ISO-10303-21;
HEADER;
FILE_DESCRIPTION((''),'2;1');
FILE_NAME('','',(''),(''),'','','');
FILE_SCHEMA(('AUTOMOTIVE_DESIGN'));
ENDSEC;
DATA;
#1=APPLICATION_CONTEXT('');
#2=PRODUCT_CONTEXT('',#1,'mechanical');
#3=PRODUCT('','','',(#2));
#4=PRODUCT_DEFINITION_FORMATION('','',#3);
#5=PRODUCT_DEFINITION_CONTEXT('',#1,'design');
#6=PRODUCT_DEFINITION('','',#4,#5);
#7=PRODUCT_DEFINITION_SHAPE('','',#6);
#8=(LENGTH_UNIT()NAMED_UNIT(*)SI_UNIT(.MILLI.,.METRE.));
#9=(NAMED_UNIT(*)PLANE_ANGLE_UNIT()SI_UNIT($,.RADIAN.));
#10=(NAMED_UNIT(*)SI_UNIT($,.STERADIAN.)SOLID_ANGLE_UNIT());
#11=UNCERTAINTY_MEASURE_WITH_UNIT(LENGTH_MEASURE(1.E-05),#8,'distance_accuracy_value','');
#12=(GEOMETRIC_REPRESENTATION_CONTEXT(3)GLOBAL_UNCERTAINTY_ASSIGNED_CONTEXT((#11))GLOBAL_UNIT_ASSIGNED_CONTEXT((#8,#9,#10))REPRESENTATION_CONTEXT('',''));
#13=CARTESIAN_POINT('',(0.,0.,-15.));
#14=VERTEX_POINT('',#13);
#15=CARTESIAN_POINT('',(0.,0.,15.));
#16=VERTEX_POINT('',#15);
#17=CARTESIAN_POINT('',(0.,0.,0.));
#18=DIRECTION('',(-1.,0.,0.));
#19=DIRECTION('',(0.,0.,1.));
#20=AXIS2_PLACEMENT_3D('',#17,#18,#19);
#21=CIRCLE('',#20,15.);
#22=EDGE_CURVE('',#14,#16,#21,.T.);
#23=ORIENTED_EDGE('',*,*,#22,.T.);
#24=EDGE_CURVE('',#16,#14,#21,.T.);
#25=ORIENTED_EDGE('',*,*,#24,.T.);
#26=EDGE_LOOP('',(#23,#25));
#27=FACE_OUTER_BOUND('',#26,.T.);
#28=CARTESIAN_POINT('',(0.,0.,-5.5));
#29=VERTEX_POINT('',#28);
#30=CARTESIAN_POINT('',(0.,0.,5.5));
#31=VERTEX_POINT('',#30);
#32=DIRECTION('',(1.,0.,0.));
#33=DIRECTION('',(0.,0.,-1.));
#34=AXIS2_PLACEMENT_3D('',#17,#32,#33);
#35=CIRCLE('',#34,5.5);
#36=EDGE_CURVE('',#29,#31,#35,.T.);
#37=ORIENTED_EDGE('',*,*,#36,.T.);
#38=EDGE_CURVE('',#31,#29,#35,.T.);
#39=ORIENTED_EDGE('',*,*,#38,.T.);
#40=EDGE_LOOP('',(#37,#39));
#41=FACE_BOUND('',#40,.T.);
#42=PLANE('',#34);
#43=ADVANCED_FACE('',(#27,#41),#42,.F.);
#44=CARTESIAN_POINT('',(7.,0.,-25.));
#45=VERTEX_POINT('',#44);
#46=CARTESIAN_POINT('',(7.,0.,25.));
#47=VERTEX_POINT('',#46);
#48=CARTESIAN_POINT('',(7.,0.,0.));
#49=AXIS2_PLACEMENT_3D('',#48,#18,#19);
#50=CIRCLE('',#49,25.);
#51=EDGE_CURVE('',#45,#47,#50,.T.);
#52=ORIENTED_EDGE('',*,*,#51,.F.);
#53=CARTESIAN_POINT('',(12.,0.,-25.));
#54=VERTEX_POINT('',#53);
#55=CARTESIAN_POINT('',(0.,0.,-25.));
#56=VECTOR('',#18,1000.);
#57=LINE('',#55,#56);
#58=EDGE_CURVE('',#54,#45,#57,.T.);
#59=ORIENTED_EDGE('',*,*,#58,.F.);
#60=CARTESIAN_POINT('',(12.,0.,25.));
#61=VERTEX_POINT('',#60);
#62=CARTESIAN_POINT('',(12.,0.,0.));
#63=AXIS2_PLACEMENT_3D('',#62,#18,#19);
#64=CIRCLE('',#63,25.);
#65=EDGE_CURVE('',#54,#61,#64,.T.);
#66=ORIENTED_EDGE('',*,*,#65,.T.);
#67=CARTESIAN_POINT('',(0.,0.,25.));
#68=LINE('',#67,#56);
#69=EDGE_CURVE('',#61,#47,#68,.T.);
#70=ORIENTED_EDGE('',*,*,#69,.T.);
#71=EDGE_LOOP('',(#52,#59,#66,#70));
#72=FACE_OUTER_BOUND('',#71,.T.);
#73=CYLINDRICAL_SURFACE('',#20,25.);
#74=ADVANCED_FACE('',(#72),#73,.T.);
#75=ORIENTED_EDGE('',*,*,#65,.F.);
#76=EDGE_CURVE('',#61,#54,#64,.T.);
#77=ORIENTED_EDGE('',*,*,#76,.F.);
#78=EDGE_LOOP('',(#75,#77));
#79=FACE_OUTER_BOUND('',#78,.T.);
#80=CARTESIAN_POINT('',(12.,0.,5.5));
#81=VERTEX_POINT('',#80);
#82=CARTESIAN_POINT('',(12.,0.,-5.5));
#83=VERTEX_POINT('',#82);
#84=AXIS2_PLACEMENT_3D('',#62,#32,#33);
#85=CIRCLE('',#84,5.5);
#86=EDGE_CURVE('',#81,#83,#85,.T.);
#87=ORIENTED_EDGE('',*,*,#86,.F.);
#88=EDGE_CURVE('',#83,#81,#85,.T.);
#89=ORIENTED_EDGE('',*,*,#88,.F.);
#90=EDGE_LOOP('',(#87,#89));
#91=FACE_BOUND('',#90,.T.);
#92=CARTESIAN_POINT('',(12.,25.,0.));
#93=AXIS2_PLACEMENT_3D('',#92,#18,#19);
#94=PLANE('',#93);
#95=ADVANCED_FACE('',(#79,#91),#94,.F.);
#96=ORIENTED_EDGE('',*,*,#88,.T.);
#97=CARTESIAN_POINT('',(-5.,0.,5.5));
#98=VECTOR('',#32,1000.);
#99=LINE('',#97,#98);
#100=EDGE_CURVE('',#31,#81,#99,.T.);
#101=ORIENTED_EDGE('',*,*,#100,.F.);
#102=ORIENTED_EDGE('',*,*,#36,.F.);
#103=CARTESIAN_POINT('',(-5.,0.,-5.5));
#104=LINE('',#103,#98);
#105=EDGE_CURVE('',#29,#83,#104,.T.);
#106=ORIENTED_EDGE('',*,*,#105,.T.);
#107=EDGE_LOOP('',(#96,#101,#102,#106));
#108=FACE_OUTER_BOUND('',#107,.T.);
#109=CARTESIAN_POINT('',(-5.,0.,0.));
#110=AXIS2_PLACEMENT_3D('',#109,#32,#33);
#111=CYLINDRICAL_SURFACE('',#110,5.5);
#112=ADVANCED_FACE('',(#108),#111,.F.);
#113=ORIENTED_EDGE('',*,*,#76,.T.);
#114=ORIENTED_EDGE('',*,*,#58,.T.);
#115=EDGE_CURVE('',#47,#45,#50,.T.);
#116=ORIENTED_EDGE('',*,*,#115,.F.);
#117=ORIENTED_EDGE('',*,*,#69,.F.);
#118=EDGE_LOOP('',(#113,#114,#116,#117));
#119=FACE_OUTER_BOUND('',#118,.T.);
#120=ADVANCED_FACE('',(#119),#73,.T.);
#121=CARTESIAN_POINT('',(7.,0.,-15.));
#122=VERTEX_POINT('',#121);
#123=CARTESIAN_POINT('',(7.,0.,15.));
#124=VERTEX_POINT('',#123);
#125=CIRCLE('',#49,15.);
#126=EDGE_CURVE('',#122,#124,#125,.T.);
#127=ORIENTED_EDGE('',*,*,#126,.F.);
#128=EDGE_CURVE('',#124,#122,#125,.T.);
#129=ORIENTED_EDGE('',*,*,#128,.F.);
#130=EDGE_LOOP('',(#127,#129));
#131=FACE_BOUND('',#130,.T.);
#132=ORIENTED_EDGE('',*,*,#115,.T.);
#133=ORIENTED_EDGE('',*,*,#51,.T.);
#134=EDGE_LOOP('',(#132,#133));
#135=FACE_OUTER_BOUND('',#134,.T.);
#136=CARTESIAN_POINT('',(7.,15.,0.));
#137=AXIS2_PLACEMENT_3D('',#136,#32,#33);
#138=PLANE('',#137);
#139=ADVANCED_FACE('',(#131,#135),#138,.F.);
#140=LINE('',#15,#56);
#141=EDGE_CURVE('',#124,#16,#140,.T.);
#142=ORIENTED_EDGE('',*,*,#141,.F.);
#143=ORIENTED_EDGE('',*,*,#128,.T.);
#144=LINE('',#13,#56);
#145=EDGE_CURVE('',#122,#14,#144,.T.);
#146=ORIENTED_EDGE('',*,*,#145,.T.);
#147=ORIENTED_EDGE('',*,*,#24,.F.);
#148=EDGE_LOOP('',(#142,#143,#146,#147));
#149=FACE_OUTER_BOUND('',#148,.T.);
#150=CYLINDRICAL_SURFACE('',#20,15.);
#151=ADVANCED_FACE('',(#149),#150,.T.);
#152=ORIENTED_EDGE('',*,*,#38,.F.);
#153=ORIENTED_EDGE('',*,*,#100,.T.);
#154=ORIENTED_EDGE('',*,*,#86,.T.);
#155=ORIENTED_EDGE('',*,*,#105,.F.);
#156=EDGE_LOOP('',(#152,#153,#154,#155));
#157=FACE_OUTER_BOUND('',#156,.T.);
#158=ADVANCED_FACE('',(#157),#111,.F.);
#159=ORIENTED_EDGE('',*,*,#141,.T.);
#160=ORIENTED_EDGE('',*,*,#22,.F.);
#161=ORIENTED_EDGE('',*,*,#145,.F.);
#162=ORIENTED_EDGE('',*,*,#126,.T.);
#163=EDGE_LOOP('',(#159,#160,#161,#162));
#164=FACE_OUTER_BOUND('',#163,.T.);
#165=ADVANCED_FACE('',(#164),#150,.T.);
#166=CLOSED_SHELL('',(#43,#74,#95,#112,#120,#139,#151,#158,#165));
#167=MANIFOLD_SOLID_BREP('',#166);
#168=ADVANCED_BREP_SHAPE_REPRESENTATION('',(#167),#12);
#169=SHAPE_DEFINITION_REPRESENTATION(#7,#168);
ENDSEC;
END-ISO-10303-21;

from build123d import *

# Parameters (mm, degrees)
SKETCH2_R          = 5.5
CUT_EXTRUDE1_DEPTH = 17


with BuildPart() as part:
    # Sketch1 → Revolve1 (revolve)
    with BuildSketch(Plane.XY, mode=Mode.PRIVATE) as revolve1_sk:
        Polygon((0, 0), (0, 15), (7, 15), (7, 25), (12, 25), (12, 0), align=None)
    revolve(revolve1_sk.sketch.rotate(Axis((0, 0, 0), (1, 0, 0)), 90), axis=Axis((0, 0, 0), (1, 0, 0)))

    # Sketch2 → Cut-Extrude1 (cut)
    with BuildSketch(Plane(origin=(12, 0, 0), x_dir=(0, 0, -1), z_dir=(1, 0, 0))):
        Circle(SKETCH2_R)
    extrude(amount=-CUT_EXTRUDE1_DEPTH, mode=Mode.SUBTRACT)


solid = part.part
